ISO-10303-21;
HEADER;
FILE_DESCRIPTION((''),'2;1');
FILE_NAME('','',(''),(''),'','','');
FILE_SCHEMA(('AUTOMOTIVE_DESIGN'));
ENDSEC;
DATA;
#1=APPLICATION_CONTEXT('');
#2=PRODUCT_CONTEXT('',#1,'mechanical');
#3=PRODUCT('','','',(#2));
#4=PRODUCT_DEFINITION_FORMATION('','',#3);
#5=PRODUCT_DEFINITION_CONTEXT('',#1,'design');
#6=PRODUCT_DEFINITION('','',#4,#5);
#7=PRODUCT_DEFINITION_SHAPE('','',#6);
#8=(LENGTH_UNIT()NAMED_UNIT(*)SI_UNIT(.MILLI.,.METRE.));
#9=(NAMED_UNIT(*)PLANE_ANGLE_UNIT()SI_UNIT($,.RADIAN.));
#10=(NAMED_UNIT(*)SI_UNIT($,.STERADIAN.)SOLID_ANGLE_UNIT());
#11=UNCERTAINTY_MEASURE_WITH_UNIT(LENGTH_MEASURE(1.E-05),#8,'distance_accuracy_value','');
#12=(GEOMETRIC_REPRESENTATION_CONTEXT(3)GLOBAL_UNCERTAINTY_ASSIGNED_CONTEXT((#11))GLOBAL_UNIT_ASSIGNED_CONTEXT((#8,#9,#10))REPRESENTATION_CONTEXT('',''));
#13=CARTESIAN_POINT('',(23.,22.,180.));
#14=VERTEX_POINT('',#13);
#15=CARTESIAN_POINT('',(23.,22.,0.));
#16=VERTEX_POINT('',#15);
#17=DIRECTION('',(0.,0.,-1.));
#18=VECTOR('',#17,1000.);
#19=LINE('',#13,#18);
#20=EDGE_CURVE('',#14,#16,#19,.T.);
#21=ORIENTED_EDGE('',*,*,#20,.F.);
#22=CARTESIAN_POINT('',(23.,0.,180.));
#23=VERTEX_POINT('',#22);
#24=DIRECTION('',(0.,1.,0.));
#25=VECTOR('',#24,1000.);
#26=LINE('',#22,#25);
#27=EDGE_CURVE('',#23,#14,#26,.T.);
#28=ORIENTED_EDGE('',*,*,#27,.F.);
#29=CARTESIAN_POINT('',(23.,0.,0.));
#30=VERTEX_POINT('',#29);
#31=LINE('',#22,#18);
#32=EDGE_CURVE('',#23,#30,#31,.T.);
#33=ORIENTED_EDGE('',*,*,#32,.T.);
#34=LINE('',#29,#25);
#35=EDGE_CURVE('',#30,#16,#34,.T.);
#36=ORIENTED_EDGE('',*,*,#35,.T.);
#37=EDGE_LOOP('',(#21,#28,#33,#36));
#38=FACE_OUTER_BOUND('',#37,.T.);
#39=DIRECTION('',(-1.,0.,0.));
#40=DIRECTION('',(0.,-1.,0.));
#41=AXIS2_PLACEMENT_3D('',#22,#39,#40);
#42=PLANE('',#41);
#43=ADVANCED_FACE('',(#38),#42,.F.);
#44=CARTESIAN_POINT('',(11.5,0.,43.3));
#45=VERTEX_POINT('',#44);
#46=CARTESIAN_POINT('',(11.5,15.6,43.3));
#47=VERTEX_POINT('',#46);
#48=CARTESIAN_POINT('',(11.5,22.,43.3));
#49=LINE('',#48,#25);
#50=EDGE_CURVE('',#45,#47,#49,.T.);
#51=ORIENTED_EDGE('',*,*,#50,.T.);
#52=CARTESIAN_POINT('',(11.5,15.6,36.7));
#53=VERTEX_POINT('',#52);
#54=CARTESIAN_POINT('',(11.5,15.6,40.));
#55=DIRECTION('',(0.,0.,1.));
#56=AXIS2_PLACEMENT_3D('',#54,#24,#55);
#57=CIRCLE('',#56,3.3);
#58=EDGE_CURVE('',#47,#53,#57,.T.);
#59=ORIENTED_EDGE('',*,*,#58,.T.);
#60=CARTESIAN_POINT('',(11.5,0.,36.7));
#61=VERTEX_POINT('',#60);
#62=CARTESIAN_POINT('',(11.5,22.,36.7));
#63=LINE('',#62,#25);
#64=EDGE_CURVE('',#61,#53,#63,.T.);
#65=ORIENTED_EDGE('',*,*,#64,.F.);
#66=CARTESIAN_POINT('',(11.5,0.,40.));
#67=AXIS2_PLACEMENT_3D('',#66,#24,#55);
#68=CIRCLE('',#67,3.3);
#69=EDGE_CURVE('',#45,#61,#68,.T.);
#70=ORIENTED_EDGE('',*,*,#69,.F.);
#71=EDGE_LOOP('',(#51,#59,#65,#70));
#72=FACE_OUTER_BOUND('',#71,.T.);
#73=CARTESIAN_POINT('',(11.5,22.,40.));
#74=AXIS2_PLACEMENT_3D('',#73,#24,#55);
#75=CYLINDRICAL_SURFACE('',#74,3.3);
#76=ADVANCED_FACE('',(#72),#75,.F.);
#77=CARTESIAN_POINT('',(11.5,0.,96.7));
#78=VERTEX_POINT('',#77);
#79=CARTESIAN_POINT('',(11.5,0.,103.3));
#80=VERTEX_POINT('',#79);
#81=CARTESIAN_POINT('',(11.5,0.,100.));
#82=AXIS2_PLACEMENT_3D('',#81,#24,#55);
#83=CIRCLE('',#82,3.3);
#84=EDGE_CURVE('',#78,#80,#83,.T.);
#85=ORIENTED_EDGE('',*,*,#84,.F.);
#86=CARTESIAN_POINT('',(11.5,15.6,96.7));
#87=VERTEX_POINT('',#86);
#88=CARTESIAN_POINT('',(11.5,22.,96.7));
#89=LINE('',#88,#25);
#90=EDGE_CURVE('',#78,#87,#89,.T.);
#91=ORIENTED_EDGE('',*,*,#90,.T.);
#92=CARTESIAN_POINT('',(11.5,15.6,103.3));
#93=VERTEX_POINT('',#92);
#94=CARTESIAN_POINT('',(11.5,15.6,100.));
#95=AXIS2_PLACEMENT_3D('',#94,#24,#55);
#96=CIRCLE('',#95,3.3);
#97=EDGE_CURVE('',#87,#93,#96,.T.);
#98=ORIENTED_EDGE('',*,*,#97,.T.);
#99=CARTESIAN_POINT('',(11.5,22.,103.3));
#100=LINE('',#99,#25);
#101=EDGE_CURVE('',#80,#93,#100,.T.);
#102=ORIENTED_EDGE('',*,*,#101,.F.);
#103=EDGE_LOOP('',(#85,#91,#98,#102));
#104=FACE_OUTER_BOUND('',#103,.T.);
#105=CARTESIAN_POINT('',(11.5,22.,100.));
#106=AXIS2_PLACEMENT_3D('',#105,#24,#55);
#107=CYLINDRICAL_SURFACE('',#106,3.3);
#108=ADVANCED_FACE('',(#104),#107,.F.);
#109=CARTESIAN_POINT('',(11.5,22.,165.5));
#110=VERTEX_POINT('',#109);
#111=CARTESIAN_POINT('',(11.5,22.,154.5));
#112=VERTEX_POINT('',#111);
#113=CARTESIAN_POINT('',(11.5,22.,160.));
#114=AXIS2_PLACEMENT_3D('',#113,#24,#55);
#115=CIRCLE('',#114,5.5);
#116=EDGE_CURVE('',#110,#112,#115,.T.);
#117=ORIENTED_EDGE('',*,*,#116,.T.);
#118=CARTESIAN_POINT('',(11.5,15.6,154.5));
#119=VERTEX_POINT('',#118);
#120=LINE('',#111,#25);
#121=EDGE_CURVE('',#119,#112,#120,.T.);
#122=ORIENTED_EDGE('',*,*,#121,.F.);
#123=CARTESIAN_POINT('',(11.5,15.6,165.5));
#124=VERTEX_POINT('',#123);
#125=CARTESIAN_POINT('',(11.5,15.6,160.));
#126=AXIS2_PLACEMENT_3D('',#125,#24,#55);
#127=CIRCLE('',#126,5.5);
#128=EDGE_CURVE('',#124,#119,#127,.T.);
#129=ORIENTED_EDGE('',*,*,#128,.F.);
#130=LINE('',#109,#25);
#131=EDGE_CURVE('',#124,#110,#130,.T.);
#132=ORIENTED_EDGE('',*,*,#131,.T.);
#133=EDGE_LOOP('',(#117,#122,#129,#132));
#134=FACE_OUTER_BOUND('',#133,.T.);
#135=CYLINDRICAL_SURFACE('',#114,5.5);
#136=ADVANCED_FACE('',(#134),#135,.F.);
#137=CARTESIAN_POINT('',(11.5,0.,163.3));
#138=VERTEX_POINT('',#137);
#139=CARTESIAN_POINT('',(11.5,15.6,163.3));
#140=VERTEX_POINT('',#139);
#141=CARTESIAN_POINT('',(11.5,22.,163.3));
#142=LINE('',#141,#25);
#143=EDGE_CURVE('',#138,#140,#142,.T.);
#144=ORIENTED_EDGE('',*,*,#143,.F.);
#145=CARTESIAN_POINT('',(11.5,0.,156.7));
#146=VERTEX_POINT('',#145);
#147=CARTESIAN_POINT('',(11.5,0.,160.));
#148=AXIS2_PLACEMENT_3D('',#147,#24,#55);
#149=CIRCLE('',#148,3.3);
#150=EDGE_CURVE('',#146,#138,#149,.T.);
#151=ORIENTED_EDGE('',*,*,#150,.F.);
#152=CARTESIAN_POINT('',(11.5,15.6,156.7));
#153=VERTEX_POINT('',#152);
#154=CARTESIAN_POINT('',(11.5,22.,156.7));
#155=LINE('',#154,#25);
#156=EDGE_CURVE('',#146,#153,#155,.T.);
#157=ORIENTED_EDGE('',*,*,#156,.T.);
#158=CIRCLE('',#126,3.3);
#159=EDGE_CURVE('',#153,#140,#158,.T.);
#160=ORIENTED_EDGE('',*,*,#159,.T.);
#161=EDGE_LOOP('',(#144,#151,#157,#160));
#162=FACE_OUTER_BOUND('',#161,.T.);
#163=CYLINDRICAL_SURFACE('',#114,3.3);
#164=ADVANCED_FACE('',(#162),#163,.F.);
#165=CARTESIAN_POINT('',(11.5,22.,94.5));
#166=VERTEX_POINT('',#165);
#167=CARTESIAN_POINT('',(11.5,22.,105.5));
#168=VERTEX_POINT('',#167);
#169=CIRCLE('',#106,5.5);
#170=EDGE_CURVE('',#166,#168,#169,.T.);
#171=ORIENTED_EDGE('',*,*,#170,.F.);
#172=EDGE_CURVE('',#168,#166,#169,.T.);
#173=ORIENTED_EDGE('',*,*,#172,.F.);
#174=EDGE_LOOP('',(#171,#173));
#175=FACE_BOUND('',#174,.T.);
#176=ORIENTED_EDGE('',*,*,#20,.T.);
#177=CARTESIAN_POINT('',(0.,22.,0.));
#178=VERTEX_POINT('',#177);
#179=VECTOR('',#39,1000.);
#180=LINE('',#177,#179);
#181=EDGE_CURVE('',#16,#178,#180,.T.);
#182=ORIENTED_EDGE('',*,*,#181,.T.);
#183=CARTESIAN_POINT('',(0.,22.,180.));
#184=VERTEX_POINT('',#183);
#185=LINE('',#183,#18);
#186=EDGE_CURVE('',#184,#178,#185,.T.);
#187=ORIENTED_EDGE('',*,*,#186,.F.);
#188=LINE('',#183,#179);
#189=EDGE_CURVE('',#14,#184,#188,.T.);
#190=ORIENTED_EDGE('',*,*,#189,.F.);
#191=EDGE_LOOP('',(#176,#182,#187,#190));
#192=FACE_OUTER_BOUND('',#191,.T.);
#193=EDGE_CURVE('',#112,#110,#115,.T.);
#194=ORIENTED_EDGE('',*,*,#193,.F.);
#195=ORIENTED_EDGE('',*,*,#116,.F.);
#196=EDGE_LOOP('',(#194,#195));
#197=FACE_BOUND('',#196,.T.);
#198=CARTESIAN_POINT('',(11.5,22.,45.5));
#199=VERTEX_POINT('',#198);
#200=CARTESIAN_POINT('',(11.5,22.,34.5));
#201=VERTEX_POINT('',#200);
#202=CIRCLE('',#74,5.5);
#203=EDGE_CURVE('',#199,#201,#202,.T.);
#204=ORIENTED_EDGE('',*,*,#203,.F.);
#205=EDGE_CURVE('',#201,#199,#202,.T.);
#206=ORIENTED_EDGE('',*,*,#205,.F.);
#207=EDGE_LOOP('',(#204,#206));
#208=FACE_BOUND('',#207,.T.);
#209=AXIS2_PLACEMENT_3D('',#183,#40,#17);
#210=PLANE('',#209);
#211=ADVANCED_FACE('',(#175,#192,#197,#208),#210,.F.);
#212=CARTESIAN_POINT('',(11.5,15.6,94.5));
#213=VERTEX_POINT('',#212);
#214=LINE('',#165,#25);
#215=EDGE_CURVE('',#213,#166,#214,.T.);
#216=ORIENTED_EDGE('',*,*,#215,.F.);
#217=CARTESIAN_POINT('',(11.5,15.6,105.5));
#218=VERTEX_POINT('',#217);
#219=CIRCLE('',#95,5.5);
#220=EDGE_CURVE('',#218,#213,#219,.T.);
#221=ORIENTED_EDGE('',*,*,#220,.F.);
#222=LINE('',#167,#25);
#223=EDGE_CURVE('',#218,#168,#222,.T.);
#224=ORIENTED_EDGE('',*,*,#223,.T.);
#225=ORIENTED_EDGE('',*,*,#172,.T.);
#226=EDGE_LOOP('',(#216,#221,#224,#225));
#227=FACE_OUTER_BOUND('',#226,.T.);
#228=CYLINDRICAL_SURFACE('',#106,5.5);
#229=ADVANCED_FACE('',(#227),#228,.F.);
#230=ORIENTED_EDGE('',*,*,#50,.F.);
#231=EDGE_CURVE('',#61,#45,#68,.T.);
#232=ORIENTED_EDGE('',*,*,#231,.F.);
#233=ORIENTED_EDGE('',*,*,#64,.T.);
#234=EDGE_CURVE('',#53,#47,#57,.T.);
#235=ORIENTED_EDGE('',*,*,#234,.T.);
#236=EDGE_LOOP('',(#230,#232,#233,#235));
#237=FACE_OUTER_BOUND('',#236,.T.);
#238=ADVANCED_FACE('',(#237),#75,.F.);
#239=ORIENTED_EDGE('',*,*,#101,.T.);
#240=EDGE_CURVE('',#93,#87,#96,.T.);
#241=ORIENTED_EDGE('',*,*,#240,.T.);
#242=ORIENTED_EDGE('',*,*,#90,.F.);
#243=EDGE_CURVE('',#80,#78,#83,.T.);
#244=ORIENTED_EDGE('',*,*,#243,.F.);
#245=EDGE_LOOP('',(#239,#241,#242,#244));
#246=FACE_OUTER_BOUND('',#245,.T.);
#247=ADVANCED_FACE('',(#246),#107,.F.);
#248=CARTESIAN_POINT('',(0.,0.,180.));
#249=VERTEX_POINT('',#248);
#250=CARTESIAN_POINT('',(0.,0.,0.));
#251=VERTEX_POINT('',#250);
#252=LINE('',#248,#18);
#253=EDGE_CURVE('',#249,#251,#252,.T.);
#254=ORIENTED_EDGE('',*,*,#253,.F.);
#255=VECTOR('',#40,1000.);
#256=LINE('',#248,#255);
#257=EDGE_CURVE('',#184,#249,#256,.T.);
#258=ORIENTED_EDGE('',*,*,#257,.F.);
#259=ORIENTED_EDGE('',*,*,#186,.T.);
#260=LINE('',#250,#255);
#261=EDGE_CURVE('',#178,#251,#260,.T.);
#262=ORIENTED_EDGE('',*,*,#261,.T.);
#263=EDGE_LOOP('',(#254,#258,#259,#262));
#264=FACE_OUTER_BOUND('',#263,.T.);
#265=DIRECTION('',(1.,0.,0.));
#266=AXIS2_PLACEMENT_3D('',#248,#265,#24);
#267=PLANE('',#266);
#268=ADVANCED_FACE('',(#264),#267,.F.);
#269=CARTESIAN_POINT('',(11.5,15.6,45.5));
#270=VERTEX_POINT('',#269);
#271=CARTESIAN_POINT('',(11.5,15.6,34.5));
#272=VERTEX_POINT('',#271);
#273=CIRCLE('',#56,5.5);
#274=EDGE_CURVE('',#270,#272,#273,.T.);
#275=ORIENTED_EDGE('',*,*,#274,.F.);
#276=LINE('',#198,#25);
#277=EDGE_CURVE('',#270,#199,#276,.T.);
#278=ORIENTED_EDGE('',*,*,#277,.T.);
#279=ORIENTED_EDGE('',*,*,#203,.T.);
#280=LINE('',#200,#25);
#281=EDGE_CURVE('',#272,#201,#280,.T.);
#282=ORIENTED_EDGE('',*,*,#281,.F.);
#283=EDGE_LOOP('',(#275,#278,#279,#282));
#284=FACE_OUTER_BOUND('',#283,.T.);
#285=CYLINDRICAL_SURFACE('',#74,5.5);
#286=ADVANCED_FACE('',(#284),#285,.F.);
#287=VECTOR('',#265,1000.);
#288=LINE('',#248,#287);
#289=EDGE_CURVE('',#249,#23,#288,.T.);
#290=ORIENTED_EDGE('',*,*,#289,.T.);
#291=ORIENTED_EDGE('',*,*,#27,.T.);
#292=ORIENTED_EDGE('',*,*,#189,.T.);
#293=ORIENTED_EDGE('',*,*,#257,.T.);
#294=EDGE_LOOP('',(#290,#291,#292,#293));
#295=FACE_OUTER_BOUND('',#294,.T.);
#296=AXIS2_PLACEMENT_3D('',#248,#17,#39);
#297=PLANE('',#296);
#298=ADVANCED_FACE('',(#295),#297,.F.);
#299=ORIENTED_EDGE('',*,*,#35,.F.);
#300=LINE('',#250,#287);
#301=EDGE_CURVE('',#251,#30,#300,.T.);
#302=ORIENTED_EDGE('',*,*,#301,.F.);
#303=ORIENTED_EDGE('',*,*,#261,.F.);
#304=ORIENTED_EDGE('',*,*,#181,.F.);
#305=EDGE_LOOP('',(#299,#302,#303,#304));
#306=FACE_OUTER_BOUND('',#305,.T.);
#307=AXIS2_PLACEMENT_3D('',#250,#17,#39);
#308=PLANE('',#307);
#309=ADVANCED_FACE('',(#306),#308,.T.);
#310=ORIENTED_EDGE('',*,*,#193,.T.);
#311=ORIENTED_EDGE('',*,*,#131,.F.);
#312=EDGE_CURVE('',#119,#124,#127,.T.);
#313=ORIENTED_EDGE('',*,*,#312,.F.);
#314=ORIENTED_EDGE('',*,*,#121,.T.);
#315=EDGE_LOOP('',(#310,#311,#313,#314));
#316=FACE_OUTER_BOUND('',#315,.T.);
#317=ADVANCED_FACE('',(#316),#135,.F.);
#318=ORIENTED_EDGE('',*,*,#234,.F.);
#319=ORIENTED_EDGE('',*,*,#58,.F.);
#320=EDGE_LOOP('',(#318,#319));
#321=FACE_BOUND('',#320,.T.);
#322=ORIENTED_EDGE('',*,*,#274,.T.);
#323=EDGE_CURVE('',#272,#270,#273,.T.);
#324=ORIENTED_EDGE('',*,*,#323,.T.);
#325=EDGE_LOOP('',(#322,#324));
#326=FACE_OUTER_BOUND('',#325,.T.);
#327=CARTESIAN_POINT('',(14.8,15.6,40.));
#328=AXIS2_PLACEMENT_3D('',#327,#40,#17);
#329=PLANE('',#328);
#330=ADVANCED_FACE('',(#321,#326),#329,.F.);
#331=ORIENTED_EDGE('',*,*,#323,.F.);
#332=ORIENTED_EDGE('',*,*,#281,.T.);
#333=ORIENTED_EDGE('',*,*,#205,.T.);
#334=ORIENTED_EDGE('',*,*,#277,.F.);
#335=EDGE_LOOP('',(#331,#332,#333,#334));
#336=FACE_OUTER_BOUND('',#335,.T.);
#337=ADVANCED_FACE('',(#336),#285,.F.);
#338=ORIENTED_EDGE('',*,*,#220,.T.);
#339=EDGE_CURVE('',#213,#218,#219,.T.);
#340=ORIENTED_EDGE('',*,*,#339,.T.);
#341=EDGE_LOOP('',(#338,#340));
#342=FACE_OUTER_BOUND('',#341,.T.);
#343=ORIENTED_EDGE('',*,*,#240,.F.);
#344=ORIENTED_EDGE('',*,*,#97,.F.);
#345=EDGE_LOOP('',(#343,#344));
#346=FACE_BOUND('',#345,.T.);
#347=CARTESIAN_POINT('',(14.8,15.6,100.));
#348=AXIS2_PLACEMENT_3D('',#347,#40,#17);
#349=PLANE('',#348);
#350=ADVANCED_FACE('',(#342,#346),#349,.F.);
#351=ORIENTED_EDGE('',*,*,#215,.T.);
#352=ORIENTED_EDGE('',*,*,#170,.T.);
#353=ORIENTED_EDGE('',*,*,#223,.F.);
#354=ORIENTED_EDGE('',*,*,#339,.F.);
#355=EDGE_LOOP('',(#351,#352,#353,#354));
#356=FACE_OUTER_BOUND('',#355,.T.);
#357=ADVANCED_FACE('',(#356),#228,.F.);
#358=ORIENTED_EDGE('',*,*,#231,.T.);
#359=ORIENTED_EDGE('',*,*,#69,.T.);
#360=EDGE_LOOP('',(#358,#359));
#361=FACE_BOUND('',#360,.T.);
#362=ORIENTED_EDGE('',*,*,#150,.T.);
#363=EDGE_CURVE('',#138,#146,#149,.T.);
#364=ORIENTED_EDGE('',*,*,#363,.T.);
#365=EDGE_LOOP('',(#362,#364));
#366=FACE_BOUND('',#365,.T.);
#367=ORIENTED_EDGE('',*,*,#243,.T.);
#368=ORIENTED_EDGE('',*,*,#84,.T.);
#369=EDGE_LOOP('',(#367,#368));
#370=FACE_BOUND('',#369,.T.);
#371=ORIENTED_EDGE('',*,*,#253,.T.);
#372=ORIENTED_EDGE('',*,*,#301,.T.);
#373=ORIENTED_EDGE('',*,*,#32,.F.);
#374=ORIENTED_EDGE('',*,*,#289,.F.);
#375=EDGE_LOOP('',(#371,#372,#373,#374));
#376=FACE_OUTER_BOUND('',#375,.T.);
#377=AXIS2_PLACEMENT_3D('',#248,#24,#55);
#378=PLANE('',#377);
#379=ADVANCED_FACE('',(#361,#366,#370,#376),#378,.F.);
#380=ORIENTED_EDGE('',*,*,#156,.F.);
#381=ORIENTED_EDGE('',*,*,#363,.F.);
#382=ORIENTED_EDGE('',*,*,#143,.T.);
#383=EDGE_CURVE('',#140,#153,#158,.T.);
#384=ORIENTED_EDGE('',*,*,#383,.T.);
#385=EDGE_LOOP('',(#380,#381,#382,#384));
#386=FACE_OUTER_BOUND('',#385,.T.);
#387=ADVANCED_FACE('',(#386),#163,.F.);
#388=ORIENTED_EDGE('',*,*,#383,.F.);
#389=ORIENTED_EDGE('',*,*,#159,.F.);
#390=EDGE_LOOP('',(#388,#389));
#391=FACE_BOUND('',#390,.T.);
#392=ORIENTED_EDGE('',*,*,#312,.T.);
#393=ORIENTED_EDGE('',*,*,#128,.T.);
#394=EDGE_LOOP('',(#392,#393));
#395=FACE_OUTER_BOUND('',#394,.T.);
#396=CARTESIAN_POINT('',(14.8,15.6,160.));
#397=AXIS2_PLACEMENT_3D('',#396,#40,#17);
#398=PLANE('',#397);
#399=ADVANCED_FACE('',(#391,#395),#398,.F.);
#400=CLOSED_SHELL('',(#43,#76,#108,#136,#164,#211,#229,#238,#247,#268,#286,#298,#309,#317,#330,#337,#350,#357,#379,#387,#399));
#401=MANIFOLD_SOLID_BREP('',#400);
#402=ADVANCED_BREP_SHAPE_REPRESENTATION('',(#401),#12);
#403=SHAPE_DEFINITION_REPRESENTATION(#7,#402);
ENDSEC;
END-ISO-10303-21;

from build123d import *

# Parameters (mm, degrees)
SKETCH_1_W                   = 23
SKETCH_1_H                   = 22
EXTRUDE_1_DEPTH              = 180
HOLE_WIZARD_M6_1_D           = 6.6
HOLE_WIZARD_M6_1_CBORE_D     = 11
HOLE_WIZARD_M6_1_CBORE_DEPTH = 6.4
PATTERN_LINEAR_1_COUNT       = 4
PATTERN_LINEAR_1_PITCH       = 60


with BuildPart() as part:
    # 草图1 → 凸台-拉伸1 (new body)
    with BuildSketch(Plane.XY):
        with Locations((11.5, 11)):
            Rectangle(SKETCH_1_W, SKETCH_1_H)
    extrude(amount=EXTRUDE_1_DEPTH)

    # M6 六角凹头螺钉的柱形沉头孔1 (through all)
    with Locations(Plane(origin=(0, 22, 0), x_dir=(1, 0, 0), z_dir=(0, 1, 0))):
        with Locations((11.5, -160)):
            hole_wizard_m6_1 = CounterBoreHole(HOLE_WIZARD_M6_1_D / 2, HOLE_WIZARD_M6_1_CBORE_D / 2, HOLE_WIZARD_M6_1_CBORE_DEPTH)

    # 阵列(线性)1: M6 六角凹头螺钉的柱形沉头孔1 ×4
    with Locations(*[(0, 0, -i * PATTERN_LINEAR_1_PITCH) for i in range(1, PATTERN_LINEAR_1_COUNT)]):
        add(hole_wizard_m6_1, mode=Mode.SUBTRACT)


solid = part.part
